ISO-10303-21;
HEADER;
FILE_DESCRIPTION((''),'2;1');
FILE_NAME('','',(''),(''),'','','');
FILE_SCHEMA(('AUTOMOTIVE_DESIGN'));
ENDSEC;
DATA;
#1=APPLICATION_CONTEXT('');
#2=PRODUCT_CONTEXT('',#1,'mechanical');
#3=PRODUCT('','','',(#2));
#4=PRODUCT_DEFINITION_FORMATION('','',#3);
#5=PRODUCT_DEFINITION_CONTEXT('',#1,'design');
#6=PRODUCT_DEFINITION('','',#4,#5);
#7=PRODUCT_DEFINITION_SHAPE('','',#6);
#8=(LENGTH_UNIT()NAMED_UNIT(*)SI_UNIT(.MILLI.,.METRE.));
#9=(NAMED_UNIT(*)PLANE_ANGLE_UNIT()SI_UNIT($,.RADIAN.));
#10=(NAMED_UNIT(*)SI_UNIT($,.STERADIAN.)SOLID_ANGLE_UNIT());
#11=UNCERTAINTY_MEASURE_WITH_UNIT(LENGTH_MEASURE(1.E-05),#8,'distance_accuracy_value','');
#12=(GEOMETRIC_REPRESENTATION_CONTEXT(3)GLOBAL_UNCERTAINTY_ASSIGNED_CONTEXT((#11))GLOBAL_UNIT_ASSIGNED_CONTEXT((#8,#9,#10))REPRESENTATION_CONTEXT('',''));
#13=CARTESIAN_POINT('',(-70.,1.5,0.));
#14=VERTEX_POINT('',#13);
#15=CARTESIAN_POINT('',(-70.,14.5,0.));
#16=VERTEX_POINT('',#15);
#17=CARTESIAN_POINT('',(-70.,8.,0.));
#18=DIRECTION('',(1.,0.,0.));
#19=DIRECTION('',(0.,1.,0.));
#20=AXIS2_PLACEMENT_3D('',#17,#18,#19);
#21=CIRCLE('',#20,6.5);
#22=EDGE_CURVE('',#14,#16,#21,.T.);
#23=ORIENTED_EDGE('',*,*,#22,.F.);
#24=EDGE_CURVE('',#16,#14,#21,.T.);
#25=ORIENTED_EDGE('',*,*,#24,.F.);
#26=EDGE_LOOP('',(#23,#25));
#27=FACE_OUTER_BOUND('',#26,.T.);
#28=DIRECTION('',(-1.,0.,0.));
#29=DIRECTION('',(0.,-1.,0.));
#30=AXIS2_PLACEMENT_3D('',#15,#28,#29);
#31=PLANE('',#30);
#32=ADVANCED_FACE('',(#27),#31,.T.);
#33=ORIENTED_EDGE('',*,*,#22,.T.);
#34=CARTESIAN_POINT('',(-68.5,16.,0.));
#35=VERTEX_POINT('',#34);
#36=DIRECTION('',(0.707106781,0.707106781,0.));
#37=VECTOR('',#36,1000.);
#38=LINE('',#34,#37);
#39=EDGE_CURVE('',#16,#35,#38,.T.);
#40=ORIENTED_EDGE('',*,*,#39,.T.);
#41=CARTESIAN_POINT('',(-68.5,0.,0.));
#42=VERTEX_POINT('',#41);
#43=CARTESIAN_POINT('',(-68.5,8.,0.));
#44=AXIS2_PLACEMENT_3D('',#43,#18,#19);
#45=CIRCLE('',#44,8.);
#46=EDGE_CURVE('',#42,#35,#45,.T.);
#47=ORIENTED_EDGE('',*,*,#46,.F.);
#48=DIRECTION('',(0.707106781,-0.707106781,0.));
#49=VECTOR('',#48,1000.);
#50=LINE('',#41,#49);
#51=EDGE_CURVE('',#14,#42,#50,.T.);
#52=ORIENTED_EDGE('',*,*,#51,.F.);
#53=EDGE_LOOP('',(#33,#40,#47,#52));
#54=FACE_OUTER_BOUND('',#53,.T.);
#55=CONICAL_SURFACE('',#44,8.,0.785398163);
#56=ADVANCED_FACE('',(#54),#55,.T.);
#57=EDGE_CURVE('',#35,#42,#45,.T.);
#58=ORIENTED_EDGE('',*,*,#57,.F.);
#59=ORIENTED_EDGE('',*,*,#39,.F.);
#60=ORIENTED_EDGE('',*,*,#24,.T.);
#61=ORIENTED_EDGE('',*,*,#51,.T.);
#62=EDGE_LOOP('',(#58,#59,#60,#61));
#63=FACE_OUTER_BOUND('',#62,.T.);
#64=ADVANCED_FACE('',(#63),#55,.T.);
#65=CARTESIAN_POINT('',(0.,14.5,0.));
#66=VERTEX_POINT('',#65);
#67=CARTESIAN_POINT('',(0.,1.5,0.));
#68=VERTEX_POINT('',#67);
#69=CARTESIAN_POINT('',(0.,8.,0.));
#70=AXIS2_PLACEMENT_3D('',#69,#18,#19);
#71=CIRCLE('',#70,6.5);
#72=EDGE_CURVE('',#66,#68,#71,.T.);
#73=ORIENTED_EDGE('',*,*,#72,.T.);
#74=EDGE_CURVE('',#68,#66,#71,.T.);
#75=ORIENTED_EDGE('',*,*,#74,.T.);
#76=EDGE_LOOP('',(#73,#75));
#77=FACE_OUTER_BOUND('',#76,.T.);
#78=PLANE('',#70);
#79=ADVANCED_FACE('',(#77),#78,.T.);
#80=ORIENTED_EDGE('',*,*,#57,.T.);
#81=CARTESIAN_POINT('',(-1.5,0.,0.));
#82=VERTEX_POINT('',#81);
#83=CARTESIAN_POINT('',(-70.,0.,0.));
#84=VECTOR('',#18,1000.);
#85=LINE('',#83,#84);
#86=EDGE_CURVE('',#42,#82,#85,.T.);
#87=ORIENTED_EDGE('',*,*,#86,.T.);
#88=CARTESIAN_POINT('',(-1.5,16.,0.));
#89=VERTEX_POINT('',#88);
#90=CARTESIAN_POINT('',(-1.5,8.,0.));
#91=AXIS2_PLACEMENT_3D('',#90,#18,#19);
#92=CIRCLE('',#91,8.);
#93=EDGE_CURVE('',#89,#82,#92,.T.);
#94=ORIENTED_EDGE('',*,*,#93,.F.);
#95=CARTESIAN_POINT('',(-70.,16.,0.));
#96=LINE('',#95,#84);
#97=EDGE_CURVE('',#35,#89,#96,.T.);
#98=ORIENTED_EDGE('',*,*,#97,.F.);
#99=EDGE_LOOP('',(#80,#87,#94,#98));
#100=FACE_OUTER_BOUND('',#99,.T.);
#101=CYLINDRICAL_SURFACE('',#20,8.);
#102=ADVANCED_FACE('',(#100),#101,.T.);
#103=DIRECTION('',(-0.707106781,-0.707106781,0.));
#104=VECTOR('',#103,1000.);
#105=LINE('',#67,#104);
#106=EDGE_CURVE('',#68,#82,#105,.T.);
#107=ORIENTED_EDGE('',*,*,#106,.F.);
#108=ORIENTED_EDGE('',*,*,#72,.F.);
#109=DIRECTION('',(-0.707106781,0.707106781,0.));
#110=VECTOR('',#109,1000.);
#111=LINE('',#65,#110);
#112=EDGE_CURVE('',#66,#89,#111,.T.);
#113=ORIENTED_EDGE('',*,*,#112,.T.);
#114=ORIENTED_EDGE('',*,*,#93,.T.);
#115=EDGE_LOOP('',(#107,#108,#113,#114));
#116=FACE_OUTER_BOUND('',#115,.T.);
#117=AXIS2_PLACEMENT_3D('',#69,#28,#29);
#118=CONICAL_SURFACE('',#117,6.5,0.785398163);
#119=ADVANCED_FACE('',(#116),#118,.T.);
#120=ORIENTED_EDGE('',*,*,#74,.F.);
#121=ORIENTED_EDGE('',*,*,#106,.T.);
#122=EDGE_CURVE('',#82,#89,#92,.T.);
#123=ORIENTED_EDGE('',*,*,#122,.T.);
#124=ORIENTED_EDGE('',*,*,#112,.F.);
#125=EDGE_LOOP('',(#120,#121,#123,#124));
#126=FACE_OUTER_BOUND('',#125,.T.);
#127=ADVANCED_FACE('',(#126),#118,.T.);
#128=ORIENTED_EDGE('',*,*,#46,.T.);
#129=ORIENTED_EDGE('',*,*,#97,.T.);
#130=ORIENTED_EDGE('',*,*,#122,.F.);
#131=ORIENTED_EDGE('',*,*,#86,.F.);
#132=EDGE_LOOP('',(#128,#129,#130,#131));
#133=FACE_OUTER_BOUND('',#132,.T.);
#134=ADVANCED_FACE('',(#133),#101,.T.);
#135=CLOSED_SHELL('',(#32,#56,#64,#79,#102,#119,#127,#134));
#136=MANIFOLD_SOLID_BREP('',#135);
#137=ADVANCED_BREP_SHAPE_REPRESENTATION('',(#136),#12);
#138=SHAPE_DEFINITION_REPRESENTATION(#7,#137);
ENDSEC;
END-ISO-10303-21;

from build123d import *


with BuildPart() as part:
    # Sketch1 → Revolve1 (revolve)
    with BuildSketch(Plane.XY):
        Polygon((-70, 14.5), (-70, 8), (0, 8), (0, 14.5), (-1.5, 16), (-68.5, 16), align=None)
    revolve(axis=Axis((-70, 8, 0), (1, 0, 0)))


solid = part.part
